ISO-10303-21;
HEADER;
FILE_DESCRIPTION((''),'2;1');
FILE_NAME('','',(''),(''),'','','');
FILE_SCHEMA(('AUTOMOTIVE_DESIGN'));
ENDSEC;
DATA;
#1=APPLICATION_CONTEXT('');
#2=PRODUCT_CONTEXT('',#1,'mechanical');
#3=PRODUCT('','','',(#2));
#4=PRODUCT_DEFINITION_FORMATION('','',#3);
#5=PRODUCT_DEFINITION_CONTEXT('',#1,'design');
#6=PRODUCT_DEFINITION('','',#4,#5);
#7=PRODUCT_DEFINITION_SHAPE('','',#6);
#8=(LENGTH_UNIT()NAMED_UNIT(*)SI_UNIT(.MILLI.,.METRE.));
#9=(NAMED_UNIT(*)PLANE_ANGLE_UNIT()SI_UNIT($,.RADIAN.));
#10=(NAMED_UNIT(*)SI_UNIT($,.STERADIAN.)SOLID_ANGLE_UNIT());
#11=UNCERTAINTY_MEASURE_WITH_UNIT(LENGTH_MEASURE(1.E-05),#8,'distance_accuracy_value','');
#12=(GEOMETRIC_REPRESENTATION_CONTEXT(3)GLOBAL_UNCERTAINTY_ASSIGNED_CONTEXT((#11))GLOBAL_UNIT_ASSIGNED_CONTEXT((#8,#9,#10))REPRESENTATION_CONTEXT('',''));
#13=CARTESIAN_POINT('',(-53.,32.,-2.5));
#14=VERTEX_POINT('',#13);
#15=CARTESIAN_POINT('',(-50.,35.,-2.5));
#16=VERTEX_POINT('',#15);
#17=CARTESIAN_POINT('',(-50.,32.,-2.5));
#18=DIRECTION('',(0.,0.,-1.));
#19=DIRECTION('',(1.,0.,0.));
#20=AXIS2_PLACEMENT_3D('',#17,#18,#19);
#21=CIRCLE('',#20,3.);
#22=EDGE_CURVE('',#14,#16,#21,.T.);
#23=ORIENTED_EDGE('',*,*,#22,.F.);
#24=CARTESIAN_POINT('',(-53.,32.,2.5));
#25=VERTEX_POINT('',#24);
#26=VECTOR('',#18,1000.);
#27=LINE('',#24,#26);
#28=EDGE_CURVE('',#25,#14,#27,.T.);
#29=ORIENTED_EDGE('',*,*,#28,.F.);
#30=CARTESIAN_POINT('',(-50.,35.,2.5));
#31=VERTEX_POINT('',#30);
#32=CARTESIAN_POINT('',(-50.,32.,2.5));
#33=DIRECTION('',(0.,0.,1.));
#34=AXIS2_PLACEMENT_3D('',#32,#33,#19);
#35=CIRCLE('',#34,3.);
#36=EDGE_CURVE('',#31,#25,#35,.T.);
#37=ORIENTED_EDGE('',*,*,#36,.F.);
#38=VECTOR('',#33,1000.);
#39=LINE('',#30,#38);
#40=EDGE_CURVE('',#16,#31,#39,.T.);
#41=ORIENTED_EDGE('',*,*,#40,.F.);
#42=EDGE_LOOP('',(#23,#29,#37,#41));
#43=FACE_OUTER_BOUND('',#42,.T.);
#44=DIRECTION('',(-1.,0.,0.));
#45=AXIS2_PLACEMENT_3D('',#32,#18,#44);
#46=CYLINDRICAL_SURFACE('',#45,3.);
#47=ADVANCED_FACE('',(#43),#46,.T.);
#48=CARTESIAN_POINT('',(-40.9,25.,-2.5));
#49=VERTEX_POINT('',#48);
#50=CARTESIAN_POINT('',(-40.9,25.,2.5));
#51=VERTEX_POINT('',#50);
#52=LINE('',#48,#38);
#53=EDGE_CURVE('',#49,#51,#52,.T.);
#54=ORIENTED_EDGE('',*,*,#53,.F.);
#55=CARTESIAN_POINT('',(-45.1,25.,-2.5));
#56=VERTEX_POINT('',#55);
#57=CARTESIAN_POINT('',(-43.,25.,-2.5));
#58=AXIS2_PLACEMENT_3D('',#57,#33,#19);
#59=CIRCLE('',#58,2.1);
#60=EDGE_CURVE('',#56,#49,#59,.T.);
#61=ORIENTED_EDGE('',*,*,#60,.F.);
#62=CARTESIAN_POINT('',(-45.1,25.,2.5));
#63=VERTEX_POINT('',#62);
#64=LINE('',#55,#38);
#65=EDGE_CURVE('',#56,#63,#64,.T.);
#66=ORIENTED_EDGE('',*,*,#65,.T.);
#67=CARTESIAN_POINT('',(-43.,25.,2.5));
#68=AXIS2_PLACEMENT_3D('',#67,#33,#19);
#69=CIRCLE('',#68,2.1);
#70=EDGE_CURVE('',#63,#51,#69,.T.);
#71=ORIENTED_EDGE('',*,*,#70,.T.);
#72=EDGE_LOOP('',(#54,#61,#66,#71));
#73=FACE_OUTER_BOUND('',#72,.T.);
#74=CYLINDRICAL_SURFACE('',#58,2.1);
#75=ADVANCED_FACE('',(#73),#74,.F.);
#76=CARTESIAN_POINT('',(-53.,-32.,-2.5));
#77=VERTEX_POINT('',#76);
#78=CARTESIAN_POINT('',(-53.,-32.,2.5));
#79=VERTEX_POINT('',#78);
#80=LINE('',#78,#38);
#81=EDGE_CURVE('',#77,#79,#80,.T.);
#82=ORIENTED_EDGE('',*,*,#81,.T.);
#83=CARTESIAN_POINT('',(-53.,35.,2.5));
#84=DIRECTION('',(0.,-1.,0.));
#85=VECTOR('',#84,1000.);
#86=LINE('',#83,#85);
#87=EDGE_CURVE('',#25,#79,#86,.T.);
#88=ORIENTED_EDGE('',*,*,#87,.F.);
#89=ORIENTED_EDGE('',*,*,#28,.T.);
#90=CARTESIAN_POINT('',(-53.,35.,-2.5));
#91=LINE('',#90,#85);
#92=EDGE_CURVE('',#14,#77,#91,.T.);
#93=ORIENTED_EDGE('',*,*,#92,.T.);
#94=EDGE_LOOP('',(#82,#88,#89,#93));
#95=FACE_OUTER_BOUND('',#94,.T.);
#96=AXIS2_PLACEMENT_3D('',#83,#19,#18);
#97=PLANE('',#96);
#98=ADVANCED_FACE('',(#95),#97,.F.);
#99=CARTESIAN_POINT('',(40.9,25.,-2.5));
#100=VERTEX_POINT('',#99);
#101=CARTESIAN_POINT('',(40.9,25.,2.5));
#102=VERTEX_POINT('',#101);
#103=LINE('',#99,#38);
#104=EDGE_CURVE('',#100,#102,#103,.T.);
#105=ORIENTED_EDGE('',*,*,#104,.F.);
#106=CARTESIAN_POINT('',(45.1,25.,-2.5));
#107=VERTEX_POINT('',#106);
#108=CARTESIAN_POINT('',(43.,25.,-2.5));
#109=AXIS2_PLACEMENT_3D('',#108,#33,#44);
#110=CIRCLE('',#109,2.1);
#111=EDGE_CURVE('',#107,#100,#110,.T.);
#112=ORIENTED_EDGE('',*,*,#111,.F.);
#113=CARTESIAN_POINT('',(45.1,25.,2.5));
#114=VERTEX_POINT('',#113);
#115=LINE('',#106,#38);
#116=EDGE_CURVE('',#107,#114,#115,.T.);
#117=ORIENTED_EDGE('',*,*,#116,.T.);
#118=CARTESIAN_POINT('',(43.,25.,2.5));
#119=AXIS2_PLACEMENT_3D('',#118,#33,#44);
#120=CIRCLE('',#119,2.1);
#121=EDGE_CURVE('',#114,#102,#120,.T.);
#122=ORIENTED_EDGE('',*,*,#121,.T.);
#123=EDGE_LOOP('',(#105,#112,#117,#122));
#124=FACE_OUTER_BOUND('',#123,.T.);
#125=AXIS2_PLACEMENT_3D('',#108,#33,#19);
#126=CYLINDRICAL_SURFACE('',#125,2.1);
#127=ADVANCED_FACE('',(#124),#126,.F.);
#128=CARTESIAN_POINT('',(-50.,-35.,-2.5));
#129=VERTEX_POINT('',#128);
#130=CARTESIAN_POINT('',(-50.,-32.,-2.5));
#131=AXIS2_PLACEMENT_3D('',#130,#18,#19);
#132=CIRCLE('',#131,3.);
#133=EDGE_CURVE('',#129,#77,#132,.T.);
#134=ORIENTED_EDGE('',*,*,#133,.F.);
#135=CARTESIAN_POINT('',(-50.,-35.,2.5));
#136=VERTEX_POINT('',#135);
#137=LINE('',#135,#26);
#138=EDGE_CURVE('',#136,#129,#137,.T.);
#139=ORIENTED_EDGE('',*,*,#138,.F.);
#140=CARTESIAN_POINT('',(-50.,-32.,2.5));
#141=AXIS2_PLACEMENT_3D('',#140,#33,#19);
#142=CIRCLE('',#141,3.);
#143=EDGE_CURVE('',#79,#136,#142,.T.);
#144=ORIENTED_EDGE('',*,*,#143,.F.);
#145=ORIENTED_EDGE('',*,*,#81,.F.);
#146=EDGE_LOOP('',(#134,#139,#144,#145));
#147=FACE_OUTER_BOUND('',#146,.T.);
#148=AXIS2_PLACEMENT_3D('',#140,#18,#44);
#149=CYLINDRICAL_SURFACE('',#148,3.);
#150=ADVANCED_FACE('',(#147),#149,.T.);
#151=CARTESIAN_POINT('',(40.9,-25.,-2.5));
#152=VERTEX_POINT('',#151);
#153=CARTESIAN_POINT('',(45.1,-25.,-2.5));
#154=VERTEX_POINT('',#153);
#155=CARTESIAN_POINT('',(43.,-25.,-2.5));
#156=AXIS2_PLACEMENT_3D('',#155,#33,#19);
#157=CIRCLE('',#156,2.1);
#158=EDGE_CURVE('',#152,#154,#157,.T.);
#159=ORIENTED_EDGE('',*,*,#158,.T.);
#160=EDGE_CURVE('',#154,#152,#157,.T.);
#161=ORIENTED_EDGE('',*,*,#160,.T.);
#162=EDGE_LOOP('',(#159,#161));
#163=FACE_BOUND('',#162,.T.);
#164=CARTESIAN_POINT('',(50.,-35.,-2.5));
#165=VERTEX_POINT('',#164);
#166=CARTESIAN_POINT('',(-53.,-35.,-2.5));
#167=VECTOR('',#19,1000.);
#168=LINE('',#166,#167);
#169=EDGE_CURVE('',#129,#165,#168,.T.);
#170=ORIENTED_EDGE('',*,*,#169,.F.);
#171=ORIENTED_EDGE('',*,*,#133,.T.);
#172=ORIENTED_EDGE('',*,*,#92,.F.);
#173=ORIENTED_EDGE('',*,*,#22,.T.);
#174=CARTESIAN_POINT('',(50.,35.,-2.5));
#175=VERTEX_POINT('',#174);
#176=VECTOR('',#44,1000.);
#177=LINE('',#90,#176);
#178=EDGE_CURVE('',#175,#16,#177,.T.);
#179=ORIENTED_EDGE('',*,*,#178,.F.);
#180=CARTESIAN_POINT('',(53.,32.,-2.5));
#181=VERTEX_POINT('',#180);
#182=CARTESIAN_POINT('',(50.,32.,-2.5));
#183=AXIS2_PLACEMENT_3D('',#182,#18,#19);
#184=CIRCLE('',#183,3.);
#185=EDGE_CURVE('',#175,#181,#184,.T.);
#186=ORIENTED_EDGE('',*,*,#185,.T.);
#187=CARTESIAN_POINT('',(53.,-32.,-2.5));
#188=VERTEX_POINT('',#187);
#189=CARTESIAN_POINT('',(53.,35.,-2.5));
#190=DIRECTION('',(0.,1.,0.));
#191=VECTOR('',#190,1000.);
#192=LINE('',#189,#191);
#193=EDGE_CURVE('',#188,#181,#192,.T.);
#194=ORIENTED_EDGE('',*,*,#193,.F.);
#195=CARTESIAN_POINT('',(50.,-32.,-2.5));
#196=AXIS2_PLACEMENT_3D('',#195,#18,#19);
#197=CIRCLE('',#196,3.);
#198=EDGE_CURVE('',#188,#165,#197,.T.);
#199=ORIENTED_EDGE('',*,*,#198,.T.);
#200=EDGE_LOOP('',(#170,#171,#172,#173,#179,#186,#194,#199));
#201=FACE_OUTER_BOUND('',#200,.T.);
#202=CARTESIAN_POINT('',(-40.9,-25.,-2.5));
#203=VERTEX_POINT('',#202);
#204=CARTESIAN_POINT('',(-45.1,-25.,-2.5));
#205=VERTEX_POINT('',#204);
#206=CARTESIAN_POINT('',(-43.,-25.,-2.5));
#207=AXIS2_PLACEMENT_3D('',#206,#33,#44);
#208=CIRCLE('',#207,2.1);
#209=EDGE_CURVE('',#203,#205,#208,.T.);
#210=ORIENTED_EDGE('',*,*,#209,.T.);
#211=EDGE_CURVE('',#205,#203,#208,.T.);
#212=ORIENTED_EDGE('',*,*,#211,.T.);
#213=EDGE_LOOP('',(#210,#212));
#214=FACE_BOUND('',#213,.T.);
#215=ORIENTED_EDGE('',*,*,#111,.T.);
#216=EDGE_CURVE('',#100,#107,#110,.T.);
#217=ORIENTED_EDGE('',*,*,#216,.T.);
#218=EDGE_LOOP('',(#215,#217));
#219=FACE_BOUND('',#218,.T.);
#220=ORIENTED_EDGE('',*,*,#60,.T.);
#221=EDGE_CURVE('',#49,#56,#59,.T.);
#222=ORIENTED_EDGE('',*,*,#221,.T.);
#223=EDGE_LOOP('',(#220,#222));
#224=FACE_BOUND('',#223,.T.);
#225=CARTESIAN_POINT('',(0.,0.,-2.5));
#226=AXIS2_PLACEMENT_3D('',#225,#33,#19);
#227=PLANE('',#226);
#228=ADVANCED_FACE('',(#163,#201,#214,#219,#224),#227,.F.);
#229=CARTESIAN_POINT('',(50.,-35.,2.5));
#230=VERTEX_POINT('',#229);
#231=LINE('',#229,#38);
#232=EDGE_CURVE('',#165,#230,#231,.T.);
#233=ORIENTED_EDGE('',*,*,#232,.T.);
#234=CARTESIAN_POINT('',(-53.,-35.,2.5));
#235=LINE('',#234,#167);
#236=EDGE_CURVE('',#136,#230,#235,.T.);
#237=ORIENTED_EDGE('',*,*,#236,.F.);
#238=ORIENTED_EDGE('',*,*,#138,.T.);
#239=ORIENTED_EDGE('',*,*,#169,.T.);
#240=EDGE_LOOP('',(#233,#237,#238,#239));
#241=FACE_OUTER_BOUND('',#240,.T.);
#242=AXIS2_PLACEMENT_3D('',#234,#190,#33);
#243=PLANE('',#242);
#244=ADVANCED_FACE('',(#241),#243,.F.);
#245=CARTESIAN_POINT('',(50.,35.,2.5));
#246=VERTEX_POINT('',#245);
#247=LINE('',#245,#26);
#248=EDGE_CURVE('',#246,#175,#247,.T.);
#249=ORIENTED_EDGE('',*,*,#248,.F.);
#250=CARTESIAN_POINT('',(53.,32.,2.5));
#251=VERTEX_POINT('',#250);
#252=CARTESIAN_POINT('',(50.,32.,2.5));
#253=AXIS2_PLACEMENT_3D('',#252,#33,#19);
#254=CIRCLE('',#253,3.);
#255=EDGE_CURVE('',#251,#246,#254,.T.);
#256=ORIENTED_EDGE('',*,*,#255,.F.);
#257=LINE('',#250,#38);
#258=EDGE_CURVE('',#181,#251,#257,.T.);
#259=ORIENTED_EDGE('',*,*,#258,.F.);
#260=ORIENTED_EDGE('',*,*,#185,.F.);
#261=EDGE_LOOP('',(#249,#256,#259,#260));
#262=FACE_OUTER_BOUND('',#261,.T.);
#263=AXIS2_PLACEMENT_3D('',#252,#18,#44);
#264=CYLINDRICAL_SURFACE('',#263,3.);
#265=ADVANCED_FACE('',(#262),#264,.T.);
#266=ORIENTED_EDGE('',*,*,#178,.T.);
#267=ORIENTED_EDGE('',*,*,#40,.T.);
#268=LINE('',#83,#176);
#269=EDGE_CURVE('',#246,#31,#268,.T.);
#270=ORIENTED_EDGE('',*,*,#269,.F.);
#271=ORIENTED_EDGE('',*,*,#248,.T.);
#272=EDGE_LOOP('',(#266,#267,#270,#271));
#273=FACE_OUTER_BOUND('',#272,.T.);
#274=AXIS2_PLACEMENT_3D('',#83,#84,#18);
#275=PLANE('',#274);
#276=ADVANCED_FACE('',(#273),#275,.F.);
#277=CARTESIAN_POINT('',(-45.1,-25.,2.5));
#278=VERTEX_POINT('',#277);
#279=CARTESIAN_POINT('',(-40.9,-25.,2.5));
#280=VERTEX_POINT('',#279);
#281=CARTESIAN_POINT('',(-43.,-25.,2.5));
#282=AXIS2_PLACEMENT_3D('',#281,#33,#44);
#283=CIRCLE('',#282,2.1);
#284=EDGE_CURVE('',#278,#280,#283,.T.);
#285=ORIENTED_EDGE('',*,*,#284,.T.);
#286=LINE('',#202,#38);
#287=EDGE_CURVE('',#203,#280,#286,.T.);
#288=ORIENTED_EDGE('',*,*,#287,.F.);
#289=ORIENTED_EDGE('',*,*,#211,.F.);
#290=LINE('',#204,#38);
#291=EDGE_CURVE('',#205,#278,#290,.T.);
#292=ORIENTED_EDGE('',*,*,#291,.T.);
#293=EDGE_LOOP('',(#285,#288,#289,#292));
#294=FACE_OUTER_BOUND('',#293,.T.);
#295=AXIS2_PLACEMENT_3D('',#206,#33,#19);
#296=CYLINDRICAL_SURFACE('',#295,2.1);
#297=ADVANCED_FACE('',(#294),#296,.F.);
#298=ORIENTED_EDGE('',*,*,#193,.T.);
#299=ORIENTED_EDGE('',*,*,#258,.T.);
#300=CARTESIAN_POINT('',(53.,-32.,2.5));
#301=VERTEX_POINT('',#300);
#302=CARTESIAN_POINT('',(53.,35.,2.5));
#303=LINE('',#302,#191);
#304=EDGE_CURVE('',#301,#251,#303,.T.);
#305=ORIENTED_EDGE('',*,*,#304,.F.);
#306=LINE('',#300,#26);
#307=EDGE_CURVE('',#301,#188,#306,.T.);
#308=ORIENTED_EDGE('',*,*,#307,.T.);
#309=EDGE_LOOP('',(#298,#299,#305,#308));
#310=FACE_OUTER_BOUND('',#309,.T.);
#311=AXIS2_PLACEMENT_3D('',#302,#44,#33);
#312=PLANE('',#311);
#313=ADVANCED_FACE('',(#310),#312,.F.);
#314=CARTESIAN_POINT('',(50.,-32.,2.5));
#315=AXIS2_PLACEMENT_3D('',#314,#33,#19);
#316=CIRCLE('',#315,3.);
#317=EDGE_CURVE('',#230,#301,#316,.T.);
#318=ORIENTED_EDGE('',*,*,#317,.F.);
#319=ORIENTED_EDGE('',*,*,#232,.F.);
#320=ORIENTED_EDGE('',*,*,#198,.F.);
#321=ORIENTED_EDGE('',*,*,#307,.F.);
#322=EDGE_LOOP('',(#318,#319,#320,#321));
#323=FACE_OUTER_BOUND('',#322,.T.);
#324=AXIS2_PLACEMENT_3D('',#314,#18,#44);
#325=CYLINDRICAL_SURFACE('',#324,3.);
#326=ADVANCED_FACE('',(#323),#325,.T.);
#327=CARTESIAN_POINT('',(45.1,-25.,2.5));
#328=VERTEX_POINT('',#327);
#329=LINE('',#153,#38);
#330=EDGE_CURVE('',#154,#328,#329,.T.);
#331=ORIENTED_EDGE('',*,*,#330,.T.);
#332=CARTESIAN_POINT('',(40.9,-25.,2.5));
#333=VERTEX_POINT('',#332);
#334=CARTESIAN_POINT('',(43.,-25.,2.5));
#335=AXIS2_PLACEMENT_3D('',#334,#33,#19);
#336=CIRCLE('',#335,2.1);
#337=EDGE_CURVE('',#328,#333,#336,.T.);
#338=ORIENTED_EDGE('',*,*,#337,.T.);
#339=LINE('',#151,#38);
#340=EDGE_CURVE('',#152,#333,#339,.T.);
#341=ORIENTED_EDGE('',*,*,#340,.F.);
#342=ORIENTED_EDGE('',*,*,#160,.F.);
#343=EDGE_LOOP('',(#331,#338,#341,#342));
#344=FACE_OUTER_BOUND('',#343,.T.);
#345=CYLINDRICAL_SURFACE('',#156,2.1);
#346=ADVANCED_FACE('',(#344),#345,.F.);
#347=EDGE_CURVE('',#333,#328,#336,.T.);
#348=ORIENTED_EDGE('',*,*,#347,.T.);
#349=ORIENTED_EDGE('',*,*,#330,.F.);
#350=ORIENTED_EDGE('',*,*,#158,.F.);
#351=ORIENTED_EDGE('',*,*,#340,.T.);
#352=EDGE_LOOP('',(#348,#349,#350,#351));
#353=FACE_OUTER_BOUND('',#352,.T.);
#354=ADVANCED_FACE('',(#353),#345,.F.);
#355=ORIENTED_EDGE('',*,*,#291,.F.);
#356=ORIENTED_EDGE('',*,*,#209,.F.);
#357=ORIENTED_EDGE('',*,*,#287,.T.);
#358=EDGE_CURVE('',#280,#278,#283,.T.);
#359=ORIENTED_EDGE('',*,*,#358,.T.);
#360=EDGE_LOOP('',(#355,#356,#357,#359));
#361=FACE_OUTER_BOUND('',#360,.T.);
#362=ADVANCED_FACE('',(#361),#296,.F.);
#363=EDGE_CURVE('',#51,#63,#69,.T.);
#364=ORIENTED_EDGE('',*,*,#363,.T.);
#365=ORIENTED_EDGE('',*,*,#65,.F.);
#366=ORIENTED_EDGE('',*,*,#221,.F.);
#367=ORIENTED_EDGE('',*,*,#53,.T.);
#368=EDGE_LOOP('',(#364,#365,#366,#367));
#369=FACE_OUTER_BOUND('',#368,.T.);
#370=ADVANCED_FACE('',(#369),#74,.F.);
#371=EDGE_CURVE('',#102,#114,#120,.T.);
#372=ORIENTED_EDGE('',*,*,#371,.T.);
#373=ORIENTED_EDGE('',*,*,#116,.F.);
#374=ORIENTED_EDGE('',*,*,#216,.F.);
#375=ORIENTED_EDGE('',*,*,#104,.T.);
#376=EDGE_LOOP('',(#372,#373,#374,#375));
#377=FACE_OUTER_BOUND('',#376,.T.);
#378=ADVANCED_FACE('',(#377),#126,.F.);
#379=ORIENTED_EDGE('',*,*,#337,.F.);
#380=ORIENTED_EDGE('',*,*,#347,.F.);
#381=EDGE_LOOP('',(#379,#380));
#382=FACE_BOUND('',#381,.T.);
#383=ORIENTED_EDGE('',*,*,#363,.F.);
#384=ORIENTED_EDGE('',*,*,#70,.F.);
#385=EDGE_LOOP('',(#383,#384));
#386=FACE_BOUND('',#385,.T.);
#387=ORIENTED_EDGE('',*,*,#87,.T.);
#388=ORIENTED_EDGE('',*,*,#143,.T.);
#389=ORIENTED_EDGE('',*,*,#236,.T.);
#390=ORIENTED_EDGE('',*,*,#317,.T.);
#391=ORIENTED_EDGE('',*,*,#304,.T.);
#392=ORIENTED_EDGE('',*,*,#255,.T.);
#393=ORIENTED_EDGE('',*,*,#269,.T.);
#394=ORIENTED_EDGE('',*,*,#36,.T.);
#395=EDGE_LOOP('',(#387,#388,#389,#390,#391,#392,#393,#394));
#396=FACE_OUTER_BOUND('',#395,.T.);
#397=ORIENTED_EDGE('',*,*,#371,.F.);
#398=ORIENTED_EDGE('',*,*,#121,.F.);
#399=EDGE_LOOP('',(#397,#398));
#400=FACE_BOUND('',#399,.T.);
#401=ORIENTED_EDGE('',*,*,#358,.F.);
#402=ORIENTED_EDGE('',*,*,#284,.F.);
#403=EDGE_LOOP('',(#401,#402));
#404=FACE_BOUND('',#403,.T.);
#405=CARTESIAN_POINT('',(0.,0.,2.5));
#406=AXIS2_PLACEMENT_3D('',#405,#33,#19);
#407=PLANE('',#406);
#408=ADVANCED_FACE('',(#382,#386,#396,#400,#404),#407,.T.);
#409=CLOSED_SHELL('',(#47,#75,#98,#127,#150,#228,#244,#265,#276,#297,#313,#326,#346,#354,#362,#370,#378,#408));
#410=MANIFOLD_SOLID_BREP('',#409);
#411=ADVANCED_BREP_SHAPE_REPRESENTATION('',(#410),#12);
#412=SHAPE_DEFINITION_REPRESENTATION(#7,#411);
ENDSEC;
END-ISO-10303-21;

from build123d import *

# Parameters (mm, degrees)
SKETCH_1_W          = 106
SKETCH_1_H          = 70
EXTRUDE_1_DEPTH     = 2.5
SKETCH_2_R          = 2.1
CUT_EXTRUDE_1_DEPTH = 64.710281745
FILLET_1_R          = 3


with BuildPart() as part:
    # 草图1 → 凸台-拉伸1 (new, symmetric)
    with BuildSketch(Plane.XY):
        Rectangle(SKETCH_1_W, SKETCH_1_H)
    extrude(amount=EXTRUDE_1_DEPTH, both=True)

    # 草图2 → 切除-拉伸1 (cut, through all)
    with BuildSketch(Plane.XY.offset(2.5)):
        with Locations((-43, 25)):
            Circle(SKETCH_2_R)
        with Locations(Location((43, 25, 0), (0, 0, 180))):
            Circle(SKETCH_2_R)
        with Locations((43, -25)):
            Circle(SKETCH_2_R)
        with Locations(Location((-43, -25, 0), (0, 0, 180))):
            Circle(SKETCH_2_R)
    extrude(amount=-CUT_EXTRUDE_1_DEPTH, mode=Mode.SUBTRACT)

    # 圆角1
    fillet_1_edges = [part.edges().sort_by_distance(p)[0] for p in [
        (53, -35, 0),
        (-53, -35, 0),
        (-53, 35, 0),
        (53, 35, 0),
    ]]
    fillet(fillet_1_edges, radius=FILLET_1_R)


solid = part.part
